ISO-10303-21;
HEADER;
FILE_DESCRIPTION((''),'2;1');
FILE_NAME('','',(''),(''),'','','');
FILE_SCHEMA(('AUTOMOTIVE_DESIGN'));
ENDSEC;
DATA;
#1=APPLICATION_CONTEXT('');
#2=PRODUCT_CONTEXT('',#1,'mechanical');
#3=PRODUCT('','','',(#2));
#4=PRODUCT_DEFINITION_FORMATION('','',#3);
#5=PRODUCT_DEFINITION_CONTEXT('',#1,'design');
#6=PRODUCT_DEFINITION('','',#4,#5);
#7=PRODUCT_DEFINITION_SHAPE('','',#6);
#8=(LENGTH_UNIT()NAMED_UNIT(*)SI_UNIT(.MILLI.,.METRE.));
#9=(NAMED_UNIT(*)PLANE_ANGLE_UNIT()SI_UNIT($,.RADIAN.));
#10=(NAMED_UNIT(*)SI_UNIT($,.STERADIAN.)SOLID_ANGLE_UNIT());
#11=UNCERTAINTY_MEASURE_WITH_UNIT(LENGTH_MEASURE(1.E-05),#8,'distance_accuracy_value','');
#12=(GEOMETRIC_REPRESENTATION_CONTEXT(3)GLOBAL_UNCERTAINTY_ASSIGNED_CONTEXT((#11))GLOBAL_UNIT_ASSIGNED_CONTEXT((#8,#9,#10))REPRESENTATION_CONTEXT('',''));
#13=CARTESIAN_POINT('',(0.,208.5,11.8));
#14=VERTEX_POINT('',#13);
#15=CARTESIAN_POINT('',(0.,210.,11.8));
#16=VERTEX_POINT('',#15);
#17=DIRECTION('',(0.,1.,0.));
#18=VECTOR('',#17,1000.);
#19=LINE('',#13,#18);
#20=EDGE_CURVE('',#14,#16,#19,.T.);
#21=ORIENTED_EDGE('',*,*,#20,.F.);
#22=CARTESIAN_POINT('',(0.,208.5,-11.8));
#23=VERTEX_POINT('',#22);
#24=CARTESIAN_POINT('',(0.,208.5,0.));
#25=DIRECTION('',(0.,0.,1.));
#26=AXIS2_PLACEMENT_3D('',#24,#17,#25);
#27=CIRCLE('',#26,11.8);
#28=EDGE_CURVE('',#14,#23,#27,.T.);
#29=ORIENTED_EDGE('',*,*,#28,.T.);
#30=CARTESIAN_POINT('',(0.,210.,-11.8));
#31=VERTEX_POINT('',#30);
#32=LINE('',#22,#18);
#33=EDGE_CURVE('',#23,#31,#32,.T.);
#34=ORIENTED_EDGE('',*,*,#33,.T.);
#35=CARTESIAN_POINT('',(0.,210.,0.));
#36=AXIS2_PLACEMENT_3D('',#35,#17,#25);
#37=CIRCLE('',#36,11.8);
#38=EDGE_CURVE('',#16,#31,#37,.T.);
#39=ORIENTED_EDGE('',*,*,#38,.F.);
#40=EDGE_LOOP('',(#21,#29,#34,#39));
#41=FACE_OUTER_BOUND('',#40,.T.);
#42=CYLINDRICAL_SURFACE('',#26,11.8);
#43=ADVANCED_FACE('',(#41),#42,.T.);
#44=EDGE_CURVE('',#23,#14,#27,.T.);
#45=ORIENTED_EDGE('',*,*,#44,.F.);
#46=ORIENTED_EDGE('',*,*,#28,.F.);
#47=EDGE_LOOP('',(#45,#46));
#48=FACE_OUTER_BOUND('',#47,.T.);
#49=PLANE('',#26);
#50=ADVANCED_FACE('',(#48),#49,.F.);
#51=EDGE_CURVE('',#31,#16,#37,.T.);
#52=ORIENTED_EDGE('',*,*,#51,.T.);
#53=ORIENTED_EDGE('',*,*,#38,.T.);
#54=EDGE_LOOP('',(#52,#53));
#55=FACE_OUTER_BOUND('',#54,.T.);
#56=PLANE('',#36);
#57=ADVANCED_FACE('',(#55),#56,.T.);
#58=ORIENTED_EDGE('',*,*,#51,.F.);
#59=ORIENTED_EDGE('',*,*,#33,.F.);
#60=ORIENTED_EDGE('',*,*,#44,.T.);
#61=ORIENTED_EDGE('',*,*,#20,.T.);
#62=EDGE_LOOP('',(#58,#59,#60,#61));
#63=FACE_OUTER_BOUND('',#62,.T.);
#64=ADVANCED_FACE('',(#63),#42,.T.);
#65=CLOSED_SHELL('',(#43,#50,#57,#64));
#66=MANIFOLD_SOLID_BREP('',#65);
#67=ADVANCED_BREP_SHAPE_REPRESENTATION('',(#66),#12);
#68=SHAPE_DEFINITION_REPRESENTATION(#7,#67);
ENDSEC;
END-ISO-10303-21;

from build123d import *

# Parameters (mm, degrees)
SKETCH1_R           = 11.8
BOSS_EXTRUDE1_DEPTH = 1.5


with BuildPart() as part:
    # Sketch1 → Boss-Extrude1 (new body)
    with BuildSketch(Plane(origin=(0, 210, 0), x_dir=(1, 0, 0), z_dir=(0, 1, 0))):
        with Locations(Location((0, 0, 0), (0, 0, 270))):
            Circle(SKETCH1_R)
    extrude(amount=-BOSS_EXTRUDE1_DEPTH)


solid = part.part
